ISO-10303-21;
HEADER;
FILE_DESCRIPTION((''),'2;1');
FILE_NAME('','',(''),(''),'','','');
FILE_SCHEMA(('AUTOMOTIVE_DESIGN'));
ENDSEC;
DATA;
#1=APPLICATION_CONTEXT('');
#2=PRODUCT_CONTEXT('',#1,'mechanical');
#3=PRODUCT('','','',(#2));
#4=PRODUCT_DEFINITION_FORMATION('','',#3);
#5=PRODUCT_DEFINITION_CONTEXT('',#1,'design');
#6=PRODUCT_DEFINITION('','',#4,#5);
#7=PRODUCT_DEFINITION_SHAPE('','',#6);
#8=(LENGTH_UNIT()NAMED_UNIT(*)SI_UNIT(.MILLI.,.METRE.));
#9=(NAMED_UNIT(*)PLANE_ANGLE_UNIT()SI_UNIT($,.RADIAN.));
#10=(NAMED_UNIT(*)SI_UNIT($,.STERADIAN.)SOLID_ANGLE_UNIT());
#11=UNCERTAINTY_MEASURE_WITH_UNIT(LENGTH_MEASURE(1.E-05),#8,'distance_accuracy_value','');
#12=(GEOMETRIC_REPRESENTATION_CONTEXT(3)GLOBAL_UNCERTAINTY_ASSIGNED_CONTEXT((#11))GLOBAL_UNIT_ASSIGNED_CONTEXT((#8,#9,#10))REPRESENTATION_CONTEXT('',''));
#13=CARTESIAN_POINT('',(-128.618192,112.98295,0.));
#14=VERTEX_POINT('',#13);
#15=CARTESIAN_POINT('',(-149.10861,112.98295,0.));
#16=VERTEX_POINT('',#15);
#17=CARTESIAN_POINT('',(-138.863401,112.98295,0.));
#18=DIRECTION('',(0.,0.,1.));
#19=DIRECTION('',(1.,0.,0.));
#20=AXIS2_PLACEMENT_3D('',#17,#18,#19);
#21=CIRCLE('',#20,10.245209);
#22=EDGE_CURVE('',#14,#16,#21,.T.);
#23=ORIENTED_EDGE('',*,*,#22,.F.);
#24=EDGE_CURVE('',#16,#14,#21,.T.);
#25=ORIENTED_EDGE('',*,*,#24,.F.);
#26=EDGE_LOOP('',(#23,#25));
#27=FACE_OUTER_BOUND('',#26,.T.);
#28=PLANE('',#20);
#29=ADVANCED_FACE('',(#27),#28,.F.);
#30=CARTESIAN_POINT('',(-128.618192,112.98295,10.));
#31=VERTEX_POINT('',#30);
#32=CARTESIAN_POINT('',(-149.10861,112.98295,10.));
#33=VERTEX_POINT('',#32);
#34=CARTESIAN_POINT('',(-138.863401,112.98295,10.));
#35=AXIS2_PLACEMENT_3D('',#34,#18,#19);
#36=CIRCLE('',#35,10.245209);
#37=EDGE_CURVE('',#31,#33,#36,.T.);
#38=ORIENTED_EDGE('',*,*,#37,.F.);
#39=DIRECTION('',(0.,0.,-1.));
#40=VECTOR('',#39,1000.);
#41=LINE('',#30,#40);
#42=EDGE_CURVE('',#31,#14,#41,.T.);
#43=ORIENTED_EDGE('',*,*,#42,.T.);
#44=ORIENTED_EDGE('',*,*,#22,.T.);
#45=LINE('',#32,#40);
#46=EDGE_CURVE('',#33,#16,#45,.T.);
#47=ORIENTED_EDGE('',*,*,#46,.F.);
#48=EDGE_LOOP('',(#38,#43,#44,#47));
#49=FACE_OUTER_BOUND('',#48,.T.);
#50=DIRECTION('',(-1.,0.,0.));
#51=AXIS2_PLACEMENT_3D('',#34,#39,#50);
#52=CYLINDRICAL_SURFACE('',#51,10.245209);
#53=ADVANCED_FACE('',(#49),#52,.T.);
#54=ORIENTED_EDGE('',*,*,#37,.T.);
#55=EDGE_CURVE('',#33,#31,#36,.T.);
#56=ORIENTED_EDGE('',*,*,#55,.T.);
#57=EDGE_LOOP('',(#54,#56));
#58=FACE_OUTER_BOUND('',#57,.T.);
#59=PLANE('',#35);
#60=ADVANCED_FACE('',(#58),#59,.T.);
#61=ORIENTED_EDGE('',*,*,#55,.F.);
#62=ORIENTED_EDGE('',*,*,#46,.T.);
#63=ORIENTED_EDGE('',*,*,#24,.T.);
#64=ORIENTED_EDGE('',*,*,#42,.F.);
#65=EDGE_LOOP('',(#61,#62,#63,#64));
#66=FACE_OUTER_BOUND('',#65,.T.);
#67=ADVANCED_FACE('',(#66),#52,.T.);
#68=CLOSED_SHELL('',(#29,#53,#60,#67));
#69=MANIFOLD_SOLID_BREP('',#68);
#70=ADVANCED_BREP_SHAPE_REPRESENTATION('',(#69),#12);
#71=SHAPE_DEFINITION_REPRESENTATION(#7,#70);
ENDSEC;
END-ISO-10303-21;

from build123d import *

# Parameters (mm, degrees)
SKETCH1_R           = 10.245209284
BOSS_EXTRUDE1_DEPTH = 10


with BuildPart() as part:
    # Sketch1 → Boss-Extrude1 (new body)
    with BuildSketch(Plane.XY):
        with Locations((-138.86340096, 112.982950077)):
            Circle(SKETCH1_R)
    extrude(amount=BOSS_EXTRUDE1_DEPTH)


solid = part.part
